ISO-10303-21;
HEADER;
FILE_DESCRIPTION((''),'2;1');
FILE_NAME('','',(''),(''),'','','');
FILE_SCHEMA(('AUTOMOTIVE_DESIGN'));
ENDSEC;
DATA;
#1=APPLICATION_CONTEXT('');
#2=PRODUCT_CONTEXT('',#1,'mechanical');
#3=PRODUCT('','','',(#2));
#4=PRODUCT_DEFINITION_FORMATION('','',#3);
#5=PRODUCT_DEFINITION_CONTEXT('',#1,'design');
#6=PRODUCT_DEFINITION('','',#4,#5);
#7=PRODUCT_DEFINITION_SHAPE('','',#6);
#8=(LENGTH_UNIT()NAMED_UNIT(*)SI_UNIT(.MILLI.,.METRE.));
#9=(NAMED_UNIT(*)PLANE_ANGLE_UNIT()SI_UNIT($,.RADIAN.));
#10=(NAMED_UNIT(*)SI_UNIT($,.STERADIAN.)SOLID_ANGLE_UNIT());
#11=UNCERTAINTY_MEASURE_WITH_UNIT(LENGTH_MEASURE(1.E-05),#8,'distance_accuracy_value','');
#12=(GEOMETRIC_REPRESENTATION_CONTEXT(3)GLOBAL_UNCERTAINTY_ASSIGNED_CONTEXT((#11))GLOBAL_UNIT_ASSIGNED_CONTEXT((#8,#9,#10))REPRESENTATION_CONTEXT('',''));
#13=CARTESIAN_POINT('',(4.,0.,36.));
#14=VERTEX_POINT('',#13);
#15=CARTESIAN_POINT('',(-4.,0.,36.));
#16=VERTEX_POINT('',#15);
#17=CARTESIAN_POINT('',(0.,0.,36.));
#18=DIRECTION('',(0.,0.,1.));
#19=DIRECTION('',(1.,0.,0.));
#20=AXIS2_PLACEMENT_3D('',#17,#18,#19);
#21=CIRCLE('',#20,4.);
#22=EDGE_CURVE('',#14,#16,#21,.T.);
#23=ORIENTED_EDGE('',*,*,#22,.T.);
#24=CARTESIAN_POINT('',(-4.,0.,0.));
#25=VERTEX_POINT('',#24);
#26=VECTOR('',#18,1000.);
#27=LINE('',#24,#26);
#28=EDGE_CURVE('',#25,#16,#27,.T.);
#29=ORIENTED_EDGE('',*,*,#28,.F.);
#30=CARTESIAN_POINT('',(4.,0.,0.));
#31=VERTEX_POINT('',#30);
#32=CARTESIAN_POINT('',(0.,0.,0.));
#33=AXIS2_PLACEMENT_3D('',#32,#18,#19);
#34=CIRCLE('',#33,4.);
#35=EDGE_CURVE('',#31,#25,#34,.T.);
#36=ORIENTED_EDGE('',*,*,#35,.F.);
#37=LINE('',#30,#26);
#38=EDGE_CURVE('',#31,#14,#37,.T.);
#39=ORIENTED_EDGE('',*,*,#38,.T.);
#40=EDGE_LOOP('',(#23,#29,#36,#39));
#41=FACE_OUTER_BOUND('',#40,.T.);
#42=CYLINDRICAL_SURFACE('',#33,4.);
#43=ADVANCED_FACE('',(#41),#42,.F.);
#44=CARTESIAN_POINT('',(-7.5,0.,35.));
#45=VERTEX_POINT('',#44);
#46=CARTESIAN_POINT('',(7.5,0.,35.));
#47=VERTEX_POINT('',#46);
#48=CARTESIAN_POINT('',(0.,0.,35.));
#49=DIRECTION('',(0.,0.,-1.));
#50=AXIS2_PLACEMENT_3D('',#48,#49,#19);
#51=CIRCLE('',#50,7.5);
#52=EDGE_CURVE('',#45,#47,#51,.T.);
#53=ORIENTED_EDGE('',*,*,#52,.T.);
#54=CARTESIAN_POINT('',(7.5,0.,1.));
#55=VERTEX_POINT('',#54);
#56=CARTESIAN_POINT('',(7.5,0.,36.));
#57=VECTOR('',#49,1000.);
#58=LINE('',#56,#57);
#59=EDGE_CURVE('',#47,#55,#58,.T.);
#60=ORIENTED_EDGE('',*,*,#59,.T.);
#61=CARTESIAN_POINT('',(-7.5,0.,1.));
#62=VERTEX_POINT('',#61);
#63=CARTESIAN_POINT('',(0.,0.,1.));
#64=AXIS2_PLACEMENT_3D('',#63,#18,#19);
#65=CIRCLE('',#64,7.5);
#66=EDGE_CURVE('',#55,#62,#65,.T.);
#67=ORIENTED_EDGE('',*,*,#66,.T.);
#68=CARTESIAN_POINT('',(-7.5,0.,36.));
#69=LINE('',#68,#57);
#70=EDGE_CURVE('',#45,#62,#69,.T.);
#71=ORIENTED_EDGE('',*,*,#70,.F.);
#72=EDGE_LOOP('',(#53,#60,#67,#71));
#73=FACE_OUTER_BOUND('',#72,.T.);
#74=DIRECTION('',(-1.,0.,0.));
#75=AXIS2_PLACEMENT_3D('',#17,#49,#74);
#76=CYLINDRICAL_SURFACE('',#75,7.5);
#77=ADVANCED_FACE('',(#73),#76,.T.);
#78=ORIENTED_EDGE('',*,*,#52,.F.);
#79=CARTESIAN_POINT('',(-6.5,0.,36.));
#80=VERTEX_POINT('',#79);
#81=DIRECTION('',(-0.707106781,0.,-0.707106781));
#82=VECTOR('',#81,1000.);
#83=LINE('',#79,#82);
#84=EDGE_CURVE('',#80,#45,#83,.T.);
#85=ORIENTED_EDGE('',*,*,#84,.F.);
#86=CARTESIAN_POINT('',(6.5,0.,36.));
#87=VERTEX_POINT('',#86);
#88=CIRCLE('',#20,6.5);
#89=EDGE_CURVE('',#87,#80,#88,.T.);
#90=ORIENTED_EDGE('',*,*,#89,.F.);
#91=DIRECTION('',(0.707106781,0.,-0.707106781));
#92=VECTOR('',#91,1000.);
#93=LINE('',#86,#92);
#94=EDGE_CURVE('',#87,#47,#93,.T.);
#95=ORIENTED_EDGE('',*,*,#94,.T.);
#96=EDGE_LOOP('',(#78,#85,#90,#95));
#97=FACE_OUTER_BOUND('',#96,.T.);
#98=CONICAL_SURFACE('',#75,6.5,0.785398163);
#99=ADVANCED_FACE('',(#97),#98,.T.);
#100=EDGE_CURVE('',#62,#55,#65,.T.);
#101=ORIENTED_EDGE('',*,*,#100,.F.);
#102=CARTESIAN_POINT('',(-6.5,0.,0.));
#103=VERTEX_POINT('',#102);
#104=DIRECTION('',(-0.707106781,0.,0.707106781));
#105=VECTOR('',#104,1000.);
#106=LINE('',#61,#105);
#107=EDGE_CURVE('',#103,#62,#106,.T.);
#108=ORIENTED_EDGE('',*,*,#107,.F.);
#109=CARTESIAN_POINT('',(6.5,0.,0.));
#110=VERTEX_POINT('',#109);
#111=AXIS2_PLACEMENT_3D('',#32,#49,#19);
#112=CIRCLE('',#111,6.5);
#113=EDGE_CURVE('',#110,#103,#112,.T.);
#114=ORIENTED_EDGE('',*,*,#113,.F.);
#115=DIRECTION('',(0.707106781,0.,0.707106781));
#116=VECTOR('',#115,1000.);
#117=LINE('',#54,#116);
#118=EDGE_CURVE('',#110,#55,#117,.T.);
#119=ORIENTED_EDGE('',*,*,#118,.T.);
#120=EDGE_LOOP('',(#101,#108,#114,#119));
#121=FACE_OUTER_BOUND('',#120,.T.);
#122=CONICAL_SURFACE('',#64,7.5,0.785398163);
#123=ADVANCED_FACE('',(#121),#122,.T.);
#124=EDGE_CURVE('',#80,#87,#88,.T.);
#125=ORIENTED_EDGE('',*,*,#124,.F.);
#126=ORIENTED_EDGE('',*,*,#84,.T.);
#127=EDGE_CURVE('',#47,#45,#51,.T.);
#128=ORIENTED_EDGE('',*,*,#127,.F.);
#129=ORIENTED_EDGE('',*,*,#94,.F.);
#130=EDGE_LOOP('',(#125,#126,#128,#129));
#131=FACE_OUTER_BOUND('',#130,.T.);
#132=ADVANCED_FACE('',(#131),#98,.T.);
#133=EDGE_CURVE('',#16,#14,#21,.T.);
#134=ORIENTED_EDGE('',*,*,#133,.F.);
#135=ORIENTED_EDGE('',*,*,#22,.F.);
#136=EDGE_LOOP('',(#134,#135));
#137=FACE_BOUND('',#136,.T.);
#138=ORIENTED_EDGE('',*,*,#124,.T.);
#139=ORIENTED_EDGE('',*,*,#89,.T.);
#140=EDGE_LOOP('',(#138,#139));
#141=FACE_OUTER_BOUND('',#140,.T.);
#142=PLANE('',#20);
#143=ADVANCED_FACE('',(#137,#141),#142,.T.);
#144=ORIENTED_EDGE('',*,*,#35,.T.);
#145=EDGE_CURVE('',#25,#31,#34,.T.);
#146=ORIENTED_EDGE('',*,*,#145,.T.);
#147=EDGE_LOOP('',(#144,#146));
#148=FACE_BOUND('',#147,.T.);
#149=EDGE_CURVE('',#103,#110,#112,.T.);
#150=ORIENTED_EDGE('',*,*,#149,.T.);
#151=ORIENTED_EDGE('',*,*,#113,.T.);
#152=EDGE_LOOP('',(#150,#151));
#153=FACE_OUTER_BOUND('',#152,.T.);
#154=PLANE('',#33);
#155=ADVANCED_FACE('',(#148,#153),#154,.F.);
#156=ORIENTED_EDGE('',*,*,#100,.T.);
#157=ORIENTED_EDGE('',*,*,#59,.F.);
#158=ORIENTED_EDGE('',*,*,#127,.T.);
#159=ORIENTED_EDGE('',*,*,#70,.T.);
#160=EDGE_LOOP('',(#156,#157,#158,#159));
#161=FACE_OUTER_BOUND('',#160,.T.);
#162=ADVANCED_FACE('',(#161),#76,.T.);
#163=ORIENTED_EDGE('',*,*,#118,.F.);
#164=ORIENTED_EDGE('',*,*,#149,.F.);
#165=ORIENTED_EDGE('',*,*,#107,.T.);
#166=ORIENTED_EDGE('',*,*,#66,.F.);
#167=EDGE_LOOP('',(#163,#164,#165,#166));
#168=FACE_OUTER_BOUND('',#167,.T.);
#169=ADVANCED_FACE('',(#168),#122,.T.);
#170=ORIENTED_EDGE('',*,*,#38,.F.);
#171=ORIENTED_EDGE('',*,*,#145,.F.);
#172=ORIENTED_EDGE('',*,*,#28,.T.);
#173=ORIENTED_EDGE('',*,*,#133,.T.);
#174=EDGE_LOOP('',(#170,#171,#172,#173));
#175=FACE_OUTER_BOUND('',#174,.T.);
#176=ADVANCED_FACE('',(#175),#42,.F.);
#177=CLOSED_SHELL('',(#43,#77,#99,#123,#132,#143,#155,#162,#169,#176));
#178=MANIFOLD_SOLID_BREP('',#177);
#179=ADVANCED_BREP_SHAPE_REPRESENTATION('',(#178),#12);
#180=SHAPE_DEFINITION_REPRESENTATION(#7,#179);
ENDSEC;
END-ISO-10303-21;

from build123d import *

# Parameters (mm, degrees)
SKETCH1_R           = 7.5
BOSS_EXTRUDE1_DEPTH = 36
CHAMFER1_SIZE       = 1
SKETCH2_R           = 4
CUT_EXTRUDE1_DEPTH  = 38.52998801


with BuildPart() as part:
    # Sketch1 → Boss-Extrude1 (new body)
    with BuildSketch(Plane.XY):
        Circle(SKETCH1_R)
    extrude(amount=BOSS_EXTRUDE1_DEPTH)

    # Chamfer1
    chamfer1_edges = [part.edges().sort_by_distance(p)[0] for p in [
        (-7.5, 0, 0),
        (-7.5, 0, 36),
    ]]
    chamfer(chamfer1_edges, length=CHAMFER1_SIZE)

    # Sketch2 → Cut-Extrude1 (cut, through all)
    with BuildSketch(Plane.XY.offset(36)):
        Circle(SKETCH2_R)
    extrude(amount=-CUT_EXTRUDE1_DEPTH, mode=Mode.SUBTRACT)


solid = part.part
